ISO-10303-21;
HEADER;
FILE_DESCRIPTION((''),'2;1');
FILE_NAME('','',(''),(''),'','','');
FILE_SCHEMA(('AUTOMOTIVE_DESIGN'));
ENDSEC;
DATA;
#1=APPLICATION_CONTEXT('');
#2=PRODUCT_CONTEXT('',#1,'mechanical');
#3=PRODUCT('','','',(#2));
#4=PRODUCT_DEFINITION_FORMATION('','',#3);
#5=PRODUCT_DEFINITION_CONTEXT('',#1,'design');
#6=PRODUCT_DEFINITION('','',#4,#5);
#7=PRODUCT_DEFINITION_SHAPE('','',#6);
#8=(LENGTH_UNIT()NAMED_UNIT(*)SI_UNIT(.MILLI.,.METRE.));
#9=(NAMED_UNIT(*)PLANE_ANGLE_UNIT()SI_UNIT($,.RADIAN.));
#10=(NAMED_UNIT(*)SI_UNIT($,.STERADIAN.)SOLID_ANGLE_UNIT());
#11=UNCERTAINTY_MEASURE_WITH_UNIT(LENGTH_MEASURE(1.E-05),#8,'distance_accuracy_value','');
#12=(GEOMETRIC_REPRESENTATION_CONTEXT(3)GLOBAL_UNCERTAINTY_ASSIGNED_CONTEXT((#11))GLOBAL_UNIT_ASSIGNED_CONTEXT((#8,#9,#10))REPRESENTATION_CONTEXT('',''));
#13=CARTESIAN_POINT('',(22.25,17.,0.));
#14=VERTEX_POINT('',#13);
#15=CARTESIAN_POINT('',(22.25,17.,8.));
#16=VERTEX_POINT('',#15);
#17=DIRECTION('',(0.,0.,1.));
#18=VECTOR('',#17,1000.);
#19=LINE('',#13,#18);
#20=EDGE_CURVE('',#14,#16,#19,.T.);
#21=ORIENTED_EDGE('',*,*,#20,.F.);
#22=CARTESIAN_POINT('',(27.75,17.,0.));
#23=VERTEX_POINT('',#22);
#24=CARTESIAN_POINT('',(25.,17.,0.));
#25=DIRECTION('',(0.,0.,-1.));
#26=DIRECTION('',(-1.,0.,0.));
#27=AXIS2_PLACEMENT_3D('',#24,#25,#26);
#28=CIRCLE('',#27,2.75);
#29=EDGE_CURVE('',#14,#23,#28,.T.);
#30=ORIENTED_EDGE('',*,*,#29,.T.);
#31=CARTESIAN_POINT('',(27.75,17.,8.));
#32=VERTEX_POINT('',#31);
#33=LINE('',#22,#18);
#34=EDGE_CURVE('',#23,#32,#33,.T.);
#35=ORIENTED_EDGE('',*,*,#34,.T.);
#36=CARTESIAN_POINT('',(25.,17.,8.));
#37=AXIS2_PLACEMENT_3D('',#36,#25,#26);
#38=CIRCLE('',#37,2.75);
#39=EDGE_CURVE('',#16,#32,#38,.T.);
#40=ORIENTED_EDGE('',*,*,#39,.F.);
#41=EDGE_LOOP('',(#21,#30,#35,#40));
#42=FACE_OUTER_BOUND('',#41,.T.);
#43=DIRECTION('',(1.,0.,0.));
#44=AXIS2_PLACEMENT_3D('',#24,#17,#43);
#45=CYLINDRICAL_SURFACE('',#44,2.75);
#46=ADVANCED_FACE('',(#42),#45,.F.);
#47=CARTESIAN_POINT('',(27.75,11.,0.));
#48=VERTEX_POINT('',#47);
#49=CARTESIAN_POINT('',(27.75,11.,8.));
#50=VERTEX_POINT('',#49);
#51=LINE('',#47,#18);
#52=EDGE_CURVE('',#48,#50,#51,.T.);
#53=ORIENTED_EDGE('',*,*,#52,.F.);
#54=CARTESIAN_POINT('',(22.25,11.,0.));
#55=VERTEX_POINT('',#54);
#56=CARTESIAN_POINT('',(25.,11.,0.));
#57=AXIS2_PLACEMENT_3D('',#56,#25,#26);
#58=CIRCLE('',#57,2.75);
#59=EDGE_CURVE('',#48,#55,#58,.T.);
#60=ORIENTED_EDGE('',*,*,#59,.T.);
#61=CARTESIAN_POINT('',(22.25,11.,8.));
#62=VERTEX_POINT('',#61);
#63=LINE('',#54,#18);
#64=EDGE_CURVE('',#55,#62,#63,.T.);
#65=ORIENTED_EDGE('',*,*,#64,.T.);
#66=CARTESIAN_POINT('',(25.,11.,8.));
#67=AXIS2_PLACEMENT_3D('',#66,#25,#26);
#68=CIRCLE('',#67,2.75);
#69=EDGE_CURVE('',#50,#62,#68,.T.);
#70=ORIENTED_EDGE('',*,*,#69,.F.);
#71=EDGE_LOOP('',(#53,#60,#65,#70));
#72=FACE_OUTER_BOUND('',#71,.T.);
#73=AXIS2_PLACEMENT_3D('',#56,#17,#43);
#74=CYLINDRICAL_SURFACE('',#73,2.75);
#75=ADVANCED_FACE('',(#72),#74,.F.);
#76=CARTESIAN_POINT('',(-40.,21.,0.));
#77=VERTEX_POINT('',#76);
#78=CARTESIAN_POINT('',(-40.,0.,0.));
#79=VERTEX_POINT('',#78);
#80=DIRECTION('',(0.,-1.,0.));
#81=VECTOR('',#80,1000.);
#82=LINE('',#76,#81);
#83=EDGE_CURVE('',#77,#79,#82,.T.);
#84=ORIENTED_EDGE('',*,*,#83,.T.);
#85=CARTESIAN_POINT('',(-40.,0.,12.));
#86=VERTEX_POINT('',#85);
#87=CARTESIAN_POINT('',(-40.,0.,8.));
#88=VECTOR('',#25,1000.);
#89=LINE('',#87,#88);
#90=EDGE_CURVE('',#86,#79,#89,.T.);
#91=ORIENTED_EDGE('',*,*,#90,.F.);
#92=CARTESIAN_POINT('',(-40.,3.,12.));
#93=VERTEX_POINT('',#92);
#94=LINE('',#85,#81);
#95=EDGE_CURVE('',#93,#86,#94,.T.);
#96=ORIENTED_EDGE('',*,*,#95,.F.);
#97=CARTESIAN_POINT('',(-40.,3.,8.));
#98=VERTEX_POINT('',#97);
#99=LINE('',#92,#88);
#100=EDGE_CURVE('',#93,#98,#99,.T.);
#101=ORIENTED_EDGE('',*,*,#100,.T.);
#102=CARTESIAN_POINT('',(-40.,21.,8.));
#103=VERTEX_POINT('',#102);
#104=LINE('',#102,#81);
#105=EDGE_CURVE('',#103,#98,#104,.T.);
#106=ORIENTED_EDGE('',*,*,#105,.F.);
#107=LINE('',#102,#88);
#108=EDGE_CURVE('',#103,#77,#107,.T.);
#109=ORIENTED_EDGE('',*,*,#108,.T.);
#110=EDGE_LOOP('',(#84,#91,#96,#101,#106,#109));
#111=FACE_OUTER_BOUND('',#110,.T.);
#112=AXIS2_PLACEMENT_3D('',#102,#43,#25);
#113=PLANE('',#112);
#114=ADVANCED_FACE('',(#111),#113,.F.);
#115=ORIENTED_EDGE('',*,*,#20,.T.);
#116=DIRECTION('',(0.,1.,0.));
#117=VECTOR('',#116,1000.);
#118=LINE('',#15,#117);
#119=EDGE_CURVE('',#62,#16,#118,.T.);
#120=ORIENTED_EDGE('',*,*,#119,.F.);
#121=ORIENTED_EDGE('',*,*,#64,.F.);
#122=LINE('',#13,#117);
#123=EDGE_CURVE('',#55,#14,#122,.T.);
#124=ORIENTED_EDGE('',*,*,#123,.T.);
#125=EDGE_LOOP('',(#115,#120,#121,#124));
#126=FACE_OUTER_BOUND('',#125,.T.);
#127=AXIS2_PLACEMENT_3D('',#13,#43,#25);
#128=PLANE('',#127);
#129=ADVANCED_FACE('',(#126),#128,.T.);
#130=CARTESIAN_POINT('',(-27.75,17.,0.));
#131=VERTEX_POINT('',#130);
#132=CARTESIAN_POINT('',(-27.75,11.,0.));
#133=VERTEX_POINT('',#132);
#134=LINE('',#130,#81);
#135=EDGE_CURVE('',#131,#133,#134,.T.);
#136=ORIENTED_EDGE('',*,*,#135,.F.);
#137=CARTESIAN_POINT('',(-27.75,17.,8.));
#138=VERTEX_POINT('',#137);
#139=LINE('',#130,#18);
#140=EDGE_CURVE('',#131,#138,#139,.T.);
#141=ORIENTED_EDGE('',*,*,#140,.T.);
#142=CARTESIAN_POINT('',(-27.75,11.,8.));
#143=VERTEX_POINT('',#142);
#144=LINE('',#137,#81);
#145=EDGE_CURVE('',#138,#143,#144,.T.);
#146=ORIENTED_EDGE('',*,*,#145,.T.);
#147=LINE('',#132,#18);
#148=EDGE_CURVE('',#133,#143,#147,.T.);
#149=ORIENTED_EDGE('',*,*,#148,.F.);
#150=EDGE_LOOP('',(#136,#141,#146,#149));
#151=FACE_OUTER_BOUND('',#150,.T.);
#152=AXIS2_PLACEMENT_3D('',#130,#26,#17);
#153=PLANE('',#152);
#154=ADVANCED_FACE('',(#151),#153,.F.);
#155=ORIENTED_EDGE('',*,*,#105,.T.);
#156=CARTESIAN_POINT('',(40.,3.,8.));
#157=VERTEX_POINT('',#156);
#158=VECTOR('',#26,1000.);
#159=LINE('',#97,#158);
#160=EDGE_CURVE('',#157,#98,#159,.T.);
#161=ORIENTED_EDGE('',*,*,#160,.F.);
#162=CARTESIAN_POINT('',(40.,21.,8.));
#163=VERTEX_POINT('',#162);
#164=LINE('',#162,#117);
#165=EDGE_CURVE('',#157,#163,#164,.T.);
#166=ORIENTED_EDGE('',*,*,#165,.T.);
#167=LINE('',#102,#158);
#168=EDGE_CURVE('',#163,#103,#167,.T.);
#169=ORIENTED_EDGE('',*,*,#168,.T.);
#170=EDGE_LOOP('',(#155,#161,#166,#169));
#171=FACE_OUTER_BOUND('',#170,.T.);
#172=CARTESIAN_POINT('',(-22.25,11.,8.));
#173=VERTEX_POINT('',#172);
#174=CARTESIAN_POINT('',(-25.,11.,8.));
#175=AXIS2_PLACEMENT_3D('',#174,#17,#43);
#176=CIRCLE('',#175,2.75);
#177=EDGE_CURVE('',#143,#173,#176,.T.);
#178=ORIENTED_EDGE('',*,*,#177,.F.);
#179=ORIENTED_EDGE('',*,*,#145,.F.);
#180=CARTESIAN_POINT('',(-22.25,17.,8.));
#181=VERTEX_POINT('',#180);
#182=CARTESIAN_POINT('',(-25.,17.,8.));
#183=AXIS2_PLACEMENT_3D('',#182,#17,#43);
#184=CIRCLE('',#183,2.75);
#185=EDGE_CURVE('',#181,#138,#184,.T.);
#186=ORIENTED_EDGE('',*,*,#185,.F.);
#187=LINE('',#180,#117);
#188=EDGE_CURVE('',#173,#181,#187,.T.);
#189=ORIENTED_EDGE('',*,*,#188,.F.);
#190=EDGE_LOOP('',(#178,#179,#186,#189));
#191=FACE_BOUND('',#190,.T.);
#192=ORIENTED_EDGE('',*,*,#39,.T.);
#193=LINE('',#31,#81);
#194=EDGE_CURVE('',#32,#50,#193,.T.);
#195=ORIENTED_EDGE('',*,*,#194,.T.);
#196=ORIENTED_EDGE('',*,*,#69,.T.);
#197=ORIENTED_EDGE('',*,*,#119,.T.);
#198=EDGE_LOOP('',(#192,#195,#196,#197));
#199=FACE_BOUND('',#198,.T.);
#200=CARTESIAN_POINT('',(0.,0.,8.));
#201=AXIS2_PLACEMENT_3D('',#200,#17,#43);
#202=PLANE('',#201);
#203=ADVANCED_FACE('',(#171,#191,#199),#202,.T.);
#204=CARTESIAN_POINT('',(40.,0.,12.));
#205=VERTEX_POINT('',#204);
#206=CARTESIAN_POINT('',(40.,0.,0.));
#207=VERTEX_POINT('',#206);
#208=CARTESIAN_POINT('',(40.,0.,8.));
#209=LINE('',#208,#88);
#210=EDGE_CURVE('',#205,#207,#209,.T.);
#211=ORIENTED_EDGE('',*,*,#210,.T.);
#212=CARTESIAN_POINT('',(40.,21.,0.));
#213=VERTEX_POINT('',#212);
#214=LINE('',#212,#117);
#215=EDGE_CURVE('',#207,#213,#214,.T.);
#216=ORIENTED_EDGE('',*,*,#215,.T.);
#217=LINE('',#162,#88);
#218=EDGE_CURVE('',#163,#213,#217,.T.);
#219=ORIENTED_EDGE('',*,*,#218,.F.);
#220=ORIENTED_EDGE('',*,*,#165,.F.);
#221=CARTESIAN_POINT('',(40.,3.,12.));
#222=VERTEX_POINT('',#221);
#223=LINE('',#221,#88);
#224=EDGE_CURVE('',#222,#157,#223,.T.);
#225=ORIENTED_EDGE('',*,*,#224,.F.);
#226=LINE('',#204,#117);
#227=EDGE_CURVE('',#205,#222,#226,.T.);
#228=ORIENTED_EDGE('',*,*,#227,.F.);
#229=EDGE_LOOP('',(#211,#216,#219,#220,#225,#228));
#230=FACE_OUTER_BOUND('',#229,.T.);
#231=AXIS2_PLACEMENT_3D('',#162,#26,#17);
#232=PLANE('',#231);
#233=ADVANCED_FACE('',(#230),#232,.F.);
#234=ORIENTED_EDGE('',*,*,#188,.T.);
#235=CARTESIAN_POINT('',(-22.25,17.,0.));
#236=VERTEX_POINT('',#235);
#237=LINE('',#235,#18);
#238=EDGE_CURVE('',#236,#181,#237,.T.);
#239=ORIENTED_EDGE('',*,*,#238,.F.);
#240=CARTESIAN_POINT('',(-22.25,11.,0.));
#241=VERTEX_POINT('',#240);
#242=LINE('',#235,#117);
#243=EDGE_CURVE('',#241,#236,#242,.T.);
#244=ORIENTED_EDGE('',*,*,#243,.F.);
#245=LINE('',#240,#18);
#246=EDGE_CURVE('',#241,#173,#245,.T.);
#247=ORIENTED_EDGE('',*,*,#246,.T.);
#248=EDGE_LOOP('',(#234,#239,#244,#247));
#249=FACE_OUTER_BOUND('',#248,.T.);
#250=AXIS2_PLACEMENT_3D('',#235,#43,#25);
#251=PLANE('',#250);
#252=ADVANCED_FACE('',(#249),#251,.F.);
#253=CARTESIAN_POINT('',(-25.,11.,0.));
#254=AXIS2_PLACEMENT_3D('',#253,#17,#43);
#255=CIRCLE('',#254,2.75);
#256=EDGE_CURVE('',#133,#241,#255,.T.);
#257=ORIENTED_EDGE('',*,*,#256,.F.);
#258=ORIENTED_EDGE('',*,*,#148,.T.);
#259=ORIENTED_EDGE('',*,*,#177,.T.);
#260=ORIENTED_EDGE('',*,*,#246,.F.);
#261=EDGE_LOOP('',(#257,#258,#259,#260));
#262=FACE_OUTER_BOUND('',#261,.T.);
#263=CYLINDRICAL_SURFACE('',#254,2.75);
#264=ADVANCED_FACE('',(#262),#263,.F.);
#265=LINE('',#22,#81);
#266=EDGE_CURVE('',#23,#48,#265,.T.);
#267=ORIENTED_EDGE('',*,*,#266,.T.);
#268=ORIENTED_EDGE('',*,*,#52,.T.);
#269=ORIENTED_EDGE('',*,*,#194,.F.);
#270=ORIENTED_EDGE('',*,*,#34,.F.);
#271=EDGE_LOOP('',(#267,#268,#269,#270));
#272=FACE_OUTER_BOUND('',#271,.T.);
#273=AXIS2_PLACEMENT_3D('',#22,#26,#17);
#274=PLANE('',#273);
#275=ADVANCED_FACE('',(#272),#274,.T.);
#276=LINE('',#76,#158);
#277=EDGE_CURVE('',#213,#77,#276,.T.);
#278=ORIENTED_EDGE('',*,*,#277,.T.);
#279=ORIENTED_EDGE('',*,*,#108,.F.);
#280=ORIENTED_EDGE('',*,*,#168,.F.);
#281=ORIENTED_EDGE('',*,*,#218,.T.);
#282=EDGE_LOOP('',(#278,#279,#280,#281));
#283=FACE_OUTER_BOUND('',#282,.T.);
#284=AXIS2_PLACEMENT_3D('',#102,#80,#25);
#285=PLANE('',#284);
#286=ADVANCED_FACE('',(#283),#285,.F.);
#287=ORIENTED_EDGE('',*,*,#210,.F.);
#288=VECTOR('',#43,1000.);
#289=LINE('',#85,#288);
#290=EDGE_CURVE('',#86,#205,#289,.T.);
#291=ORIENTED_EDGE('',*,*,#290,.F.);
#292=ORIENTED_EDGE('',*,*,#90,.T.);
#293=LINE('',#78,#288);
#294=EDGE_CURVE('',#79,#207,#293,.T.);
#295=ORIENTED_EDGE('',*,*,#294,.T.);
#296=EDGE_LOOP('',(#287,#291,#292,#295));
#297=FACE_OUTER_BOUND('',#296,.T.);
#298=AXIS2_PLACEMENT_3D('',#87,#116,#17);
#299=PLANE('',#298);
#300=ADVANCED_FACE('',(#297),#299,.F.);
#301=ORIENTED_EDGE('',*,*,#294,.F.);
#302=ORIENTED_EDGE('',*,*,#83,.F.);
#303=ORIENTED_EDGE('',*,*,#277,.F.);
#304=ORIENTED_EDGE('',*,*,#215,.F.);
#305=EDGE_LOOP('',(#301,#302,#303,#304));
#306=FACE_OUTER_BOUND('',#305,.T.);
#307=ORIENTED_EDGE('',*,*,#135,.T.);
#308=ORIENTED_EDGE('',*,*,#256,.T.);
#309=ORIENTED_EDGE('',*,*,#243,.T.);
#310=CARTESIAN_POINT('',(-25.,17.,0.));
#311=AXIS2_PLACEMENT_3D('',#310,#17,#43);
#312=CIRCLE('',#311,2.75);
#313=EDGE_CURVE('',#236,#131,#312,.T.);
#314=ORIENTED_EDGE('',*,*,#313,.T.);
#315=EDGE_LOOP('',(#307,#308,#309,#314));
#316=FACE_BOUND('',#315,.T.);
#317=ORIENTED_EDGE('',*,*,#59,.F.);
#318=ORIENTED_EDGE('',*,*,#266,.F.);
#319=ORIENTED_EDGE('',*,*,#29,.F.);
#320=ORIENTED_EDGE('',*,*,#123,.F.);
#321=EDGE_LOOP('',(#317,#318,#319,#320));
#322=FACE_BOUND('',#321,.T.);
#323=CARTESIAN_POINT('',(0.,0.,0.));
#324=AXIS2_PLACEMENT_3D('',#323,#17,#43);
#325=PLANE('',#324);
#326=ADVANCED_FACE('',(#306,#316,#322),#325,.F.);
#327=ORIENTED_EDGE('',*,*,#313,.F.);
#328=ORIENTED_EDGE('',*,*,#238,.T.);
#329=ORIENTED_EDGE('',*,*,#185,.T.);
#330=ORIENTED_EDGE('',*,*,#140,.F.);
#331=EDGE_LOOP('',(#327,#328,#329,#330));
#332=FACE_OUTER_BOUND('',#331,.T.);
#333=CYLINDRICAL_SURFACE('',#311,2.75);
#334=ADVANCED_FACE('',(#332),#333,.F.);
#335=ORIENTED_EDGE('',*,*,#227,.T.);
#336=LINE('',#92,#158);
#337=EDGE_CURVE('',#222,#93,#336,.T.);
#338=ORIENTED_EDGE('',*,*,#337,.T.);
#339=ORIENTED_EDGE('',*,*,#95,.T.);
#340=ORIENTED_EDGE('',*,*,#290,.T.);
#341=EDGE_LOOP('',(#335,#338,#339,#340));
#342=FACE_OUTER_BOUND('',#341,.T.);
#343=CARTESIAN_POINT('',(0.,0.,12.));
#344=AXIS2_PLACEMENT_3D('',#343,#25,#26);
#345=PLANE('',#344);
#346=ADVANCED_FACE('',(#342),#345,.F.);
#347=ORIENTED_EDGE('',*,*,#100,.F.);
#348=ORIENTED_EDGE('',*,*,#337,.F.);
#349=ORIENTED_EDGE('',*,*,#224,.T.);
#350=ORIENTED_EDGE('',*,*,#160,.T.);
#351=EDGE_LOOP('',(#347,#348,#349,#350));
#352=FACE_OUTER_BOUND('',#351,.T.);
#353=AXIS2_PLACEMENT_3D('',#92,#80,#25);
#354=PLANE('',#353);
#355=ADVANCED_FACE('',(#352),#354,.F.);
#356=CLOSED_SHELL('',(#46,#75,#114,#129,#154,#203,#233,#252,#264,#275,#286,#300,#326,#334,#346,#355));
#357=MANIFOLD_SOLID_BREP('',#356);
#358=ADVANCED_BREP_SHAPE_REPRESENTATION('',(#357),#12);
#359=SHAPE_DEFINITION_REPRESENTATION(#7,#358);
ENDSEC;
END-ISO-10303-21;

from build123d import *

# Parameters (mm, degrees)
SKETCH_1_W          = 80
SKETCH_1_H          = 21
EXTRUDE_1_DEPTH     = 8
SKETCH_2_W          = 80
SKETCH_2_H          = 3
EXTRUDE_2_DEPTH     = 4
CUT_EXTRUDE_1_DEPTH = 8


with BuildPart() as part:
    # 草图1 → 凸台-拉伸1 (new body)
    with BuildSketch(Plane.XY):
        with Locations((0, 10.5)):
            Rectangle(SKETCH_1_W, SKETCH_1_H)
    extrude(amount=EXTRUDE_1_DEPTH)

    # 草图2 → 凸台-拉伸2 (add)
    with BuildSketch(Plane.XY.offset(8)):
        with Locations((0, 1.5)):
            Rectangle(SKETCH_2_W, SKETCH_2_H)
    extrude(amount=EXTRUDE_2_DEPTH)

    # 草图3 → 切除-拉伸1 (cut)
    with BuildSketch(Plane.XY.offset(8)):
        with BuildLine():
            Line((-22.25, 17), (-22.25, 11))
            ThreePointArc((-22.25, 11), (-25, 8.25), (-27.75, 11))
            Line((-27.75, 11), (-27.75, 17))
            ThreePointArc((-27.75, 17), (-25, 19.75), (-22.25, 17))
        make_face()
    cut_extrude_1 = extrude(amount=-CUT_EXTRUDE_1_DEPTH, mode=Mode.SUBTRACT)

    # 镜向1: 切除-拉伸1 across plane
    add(cut_extrude_1.mirror(Plane.ZY), mode=Mode.SUBTRACT)


solid = part.part
